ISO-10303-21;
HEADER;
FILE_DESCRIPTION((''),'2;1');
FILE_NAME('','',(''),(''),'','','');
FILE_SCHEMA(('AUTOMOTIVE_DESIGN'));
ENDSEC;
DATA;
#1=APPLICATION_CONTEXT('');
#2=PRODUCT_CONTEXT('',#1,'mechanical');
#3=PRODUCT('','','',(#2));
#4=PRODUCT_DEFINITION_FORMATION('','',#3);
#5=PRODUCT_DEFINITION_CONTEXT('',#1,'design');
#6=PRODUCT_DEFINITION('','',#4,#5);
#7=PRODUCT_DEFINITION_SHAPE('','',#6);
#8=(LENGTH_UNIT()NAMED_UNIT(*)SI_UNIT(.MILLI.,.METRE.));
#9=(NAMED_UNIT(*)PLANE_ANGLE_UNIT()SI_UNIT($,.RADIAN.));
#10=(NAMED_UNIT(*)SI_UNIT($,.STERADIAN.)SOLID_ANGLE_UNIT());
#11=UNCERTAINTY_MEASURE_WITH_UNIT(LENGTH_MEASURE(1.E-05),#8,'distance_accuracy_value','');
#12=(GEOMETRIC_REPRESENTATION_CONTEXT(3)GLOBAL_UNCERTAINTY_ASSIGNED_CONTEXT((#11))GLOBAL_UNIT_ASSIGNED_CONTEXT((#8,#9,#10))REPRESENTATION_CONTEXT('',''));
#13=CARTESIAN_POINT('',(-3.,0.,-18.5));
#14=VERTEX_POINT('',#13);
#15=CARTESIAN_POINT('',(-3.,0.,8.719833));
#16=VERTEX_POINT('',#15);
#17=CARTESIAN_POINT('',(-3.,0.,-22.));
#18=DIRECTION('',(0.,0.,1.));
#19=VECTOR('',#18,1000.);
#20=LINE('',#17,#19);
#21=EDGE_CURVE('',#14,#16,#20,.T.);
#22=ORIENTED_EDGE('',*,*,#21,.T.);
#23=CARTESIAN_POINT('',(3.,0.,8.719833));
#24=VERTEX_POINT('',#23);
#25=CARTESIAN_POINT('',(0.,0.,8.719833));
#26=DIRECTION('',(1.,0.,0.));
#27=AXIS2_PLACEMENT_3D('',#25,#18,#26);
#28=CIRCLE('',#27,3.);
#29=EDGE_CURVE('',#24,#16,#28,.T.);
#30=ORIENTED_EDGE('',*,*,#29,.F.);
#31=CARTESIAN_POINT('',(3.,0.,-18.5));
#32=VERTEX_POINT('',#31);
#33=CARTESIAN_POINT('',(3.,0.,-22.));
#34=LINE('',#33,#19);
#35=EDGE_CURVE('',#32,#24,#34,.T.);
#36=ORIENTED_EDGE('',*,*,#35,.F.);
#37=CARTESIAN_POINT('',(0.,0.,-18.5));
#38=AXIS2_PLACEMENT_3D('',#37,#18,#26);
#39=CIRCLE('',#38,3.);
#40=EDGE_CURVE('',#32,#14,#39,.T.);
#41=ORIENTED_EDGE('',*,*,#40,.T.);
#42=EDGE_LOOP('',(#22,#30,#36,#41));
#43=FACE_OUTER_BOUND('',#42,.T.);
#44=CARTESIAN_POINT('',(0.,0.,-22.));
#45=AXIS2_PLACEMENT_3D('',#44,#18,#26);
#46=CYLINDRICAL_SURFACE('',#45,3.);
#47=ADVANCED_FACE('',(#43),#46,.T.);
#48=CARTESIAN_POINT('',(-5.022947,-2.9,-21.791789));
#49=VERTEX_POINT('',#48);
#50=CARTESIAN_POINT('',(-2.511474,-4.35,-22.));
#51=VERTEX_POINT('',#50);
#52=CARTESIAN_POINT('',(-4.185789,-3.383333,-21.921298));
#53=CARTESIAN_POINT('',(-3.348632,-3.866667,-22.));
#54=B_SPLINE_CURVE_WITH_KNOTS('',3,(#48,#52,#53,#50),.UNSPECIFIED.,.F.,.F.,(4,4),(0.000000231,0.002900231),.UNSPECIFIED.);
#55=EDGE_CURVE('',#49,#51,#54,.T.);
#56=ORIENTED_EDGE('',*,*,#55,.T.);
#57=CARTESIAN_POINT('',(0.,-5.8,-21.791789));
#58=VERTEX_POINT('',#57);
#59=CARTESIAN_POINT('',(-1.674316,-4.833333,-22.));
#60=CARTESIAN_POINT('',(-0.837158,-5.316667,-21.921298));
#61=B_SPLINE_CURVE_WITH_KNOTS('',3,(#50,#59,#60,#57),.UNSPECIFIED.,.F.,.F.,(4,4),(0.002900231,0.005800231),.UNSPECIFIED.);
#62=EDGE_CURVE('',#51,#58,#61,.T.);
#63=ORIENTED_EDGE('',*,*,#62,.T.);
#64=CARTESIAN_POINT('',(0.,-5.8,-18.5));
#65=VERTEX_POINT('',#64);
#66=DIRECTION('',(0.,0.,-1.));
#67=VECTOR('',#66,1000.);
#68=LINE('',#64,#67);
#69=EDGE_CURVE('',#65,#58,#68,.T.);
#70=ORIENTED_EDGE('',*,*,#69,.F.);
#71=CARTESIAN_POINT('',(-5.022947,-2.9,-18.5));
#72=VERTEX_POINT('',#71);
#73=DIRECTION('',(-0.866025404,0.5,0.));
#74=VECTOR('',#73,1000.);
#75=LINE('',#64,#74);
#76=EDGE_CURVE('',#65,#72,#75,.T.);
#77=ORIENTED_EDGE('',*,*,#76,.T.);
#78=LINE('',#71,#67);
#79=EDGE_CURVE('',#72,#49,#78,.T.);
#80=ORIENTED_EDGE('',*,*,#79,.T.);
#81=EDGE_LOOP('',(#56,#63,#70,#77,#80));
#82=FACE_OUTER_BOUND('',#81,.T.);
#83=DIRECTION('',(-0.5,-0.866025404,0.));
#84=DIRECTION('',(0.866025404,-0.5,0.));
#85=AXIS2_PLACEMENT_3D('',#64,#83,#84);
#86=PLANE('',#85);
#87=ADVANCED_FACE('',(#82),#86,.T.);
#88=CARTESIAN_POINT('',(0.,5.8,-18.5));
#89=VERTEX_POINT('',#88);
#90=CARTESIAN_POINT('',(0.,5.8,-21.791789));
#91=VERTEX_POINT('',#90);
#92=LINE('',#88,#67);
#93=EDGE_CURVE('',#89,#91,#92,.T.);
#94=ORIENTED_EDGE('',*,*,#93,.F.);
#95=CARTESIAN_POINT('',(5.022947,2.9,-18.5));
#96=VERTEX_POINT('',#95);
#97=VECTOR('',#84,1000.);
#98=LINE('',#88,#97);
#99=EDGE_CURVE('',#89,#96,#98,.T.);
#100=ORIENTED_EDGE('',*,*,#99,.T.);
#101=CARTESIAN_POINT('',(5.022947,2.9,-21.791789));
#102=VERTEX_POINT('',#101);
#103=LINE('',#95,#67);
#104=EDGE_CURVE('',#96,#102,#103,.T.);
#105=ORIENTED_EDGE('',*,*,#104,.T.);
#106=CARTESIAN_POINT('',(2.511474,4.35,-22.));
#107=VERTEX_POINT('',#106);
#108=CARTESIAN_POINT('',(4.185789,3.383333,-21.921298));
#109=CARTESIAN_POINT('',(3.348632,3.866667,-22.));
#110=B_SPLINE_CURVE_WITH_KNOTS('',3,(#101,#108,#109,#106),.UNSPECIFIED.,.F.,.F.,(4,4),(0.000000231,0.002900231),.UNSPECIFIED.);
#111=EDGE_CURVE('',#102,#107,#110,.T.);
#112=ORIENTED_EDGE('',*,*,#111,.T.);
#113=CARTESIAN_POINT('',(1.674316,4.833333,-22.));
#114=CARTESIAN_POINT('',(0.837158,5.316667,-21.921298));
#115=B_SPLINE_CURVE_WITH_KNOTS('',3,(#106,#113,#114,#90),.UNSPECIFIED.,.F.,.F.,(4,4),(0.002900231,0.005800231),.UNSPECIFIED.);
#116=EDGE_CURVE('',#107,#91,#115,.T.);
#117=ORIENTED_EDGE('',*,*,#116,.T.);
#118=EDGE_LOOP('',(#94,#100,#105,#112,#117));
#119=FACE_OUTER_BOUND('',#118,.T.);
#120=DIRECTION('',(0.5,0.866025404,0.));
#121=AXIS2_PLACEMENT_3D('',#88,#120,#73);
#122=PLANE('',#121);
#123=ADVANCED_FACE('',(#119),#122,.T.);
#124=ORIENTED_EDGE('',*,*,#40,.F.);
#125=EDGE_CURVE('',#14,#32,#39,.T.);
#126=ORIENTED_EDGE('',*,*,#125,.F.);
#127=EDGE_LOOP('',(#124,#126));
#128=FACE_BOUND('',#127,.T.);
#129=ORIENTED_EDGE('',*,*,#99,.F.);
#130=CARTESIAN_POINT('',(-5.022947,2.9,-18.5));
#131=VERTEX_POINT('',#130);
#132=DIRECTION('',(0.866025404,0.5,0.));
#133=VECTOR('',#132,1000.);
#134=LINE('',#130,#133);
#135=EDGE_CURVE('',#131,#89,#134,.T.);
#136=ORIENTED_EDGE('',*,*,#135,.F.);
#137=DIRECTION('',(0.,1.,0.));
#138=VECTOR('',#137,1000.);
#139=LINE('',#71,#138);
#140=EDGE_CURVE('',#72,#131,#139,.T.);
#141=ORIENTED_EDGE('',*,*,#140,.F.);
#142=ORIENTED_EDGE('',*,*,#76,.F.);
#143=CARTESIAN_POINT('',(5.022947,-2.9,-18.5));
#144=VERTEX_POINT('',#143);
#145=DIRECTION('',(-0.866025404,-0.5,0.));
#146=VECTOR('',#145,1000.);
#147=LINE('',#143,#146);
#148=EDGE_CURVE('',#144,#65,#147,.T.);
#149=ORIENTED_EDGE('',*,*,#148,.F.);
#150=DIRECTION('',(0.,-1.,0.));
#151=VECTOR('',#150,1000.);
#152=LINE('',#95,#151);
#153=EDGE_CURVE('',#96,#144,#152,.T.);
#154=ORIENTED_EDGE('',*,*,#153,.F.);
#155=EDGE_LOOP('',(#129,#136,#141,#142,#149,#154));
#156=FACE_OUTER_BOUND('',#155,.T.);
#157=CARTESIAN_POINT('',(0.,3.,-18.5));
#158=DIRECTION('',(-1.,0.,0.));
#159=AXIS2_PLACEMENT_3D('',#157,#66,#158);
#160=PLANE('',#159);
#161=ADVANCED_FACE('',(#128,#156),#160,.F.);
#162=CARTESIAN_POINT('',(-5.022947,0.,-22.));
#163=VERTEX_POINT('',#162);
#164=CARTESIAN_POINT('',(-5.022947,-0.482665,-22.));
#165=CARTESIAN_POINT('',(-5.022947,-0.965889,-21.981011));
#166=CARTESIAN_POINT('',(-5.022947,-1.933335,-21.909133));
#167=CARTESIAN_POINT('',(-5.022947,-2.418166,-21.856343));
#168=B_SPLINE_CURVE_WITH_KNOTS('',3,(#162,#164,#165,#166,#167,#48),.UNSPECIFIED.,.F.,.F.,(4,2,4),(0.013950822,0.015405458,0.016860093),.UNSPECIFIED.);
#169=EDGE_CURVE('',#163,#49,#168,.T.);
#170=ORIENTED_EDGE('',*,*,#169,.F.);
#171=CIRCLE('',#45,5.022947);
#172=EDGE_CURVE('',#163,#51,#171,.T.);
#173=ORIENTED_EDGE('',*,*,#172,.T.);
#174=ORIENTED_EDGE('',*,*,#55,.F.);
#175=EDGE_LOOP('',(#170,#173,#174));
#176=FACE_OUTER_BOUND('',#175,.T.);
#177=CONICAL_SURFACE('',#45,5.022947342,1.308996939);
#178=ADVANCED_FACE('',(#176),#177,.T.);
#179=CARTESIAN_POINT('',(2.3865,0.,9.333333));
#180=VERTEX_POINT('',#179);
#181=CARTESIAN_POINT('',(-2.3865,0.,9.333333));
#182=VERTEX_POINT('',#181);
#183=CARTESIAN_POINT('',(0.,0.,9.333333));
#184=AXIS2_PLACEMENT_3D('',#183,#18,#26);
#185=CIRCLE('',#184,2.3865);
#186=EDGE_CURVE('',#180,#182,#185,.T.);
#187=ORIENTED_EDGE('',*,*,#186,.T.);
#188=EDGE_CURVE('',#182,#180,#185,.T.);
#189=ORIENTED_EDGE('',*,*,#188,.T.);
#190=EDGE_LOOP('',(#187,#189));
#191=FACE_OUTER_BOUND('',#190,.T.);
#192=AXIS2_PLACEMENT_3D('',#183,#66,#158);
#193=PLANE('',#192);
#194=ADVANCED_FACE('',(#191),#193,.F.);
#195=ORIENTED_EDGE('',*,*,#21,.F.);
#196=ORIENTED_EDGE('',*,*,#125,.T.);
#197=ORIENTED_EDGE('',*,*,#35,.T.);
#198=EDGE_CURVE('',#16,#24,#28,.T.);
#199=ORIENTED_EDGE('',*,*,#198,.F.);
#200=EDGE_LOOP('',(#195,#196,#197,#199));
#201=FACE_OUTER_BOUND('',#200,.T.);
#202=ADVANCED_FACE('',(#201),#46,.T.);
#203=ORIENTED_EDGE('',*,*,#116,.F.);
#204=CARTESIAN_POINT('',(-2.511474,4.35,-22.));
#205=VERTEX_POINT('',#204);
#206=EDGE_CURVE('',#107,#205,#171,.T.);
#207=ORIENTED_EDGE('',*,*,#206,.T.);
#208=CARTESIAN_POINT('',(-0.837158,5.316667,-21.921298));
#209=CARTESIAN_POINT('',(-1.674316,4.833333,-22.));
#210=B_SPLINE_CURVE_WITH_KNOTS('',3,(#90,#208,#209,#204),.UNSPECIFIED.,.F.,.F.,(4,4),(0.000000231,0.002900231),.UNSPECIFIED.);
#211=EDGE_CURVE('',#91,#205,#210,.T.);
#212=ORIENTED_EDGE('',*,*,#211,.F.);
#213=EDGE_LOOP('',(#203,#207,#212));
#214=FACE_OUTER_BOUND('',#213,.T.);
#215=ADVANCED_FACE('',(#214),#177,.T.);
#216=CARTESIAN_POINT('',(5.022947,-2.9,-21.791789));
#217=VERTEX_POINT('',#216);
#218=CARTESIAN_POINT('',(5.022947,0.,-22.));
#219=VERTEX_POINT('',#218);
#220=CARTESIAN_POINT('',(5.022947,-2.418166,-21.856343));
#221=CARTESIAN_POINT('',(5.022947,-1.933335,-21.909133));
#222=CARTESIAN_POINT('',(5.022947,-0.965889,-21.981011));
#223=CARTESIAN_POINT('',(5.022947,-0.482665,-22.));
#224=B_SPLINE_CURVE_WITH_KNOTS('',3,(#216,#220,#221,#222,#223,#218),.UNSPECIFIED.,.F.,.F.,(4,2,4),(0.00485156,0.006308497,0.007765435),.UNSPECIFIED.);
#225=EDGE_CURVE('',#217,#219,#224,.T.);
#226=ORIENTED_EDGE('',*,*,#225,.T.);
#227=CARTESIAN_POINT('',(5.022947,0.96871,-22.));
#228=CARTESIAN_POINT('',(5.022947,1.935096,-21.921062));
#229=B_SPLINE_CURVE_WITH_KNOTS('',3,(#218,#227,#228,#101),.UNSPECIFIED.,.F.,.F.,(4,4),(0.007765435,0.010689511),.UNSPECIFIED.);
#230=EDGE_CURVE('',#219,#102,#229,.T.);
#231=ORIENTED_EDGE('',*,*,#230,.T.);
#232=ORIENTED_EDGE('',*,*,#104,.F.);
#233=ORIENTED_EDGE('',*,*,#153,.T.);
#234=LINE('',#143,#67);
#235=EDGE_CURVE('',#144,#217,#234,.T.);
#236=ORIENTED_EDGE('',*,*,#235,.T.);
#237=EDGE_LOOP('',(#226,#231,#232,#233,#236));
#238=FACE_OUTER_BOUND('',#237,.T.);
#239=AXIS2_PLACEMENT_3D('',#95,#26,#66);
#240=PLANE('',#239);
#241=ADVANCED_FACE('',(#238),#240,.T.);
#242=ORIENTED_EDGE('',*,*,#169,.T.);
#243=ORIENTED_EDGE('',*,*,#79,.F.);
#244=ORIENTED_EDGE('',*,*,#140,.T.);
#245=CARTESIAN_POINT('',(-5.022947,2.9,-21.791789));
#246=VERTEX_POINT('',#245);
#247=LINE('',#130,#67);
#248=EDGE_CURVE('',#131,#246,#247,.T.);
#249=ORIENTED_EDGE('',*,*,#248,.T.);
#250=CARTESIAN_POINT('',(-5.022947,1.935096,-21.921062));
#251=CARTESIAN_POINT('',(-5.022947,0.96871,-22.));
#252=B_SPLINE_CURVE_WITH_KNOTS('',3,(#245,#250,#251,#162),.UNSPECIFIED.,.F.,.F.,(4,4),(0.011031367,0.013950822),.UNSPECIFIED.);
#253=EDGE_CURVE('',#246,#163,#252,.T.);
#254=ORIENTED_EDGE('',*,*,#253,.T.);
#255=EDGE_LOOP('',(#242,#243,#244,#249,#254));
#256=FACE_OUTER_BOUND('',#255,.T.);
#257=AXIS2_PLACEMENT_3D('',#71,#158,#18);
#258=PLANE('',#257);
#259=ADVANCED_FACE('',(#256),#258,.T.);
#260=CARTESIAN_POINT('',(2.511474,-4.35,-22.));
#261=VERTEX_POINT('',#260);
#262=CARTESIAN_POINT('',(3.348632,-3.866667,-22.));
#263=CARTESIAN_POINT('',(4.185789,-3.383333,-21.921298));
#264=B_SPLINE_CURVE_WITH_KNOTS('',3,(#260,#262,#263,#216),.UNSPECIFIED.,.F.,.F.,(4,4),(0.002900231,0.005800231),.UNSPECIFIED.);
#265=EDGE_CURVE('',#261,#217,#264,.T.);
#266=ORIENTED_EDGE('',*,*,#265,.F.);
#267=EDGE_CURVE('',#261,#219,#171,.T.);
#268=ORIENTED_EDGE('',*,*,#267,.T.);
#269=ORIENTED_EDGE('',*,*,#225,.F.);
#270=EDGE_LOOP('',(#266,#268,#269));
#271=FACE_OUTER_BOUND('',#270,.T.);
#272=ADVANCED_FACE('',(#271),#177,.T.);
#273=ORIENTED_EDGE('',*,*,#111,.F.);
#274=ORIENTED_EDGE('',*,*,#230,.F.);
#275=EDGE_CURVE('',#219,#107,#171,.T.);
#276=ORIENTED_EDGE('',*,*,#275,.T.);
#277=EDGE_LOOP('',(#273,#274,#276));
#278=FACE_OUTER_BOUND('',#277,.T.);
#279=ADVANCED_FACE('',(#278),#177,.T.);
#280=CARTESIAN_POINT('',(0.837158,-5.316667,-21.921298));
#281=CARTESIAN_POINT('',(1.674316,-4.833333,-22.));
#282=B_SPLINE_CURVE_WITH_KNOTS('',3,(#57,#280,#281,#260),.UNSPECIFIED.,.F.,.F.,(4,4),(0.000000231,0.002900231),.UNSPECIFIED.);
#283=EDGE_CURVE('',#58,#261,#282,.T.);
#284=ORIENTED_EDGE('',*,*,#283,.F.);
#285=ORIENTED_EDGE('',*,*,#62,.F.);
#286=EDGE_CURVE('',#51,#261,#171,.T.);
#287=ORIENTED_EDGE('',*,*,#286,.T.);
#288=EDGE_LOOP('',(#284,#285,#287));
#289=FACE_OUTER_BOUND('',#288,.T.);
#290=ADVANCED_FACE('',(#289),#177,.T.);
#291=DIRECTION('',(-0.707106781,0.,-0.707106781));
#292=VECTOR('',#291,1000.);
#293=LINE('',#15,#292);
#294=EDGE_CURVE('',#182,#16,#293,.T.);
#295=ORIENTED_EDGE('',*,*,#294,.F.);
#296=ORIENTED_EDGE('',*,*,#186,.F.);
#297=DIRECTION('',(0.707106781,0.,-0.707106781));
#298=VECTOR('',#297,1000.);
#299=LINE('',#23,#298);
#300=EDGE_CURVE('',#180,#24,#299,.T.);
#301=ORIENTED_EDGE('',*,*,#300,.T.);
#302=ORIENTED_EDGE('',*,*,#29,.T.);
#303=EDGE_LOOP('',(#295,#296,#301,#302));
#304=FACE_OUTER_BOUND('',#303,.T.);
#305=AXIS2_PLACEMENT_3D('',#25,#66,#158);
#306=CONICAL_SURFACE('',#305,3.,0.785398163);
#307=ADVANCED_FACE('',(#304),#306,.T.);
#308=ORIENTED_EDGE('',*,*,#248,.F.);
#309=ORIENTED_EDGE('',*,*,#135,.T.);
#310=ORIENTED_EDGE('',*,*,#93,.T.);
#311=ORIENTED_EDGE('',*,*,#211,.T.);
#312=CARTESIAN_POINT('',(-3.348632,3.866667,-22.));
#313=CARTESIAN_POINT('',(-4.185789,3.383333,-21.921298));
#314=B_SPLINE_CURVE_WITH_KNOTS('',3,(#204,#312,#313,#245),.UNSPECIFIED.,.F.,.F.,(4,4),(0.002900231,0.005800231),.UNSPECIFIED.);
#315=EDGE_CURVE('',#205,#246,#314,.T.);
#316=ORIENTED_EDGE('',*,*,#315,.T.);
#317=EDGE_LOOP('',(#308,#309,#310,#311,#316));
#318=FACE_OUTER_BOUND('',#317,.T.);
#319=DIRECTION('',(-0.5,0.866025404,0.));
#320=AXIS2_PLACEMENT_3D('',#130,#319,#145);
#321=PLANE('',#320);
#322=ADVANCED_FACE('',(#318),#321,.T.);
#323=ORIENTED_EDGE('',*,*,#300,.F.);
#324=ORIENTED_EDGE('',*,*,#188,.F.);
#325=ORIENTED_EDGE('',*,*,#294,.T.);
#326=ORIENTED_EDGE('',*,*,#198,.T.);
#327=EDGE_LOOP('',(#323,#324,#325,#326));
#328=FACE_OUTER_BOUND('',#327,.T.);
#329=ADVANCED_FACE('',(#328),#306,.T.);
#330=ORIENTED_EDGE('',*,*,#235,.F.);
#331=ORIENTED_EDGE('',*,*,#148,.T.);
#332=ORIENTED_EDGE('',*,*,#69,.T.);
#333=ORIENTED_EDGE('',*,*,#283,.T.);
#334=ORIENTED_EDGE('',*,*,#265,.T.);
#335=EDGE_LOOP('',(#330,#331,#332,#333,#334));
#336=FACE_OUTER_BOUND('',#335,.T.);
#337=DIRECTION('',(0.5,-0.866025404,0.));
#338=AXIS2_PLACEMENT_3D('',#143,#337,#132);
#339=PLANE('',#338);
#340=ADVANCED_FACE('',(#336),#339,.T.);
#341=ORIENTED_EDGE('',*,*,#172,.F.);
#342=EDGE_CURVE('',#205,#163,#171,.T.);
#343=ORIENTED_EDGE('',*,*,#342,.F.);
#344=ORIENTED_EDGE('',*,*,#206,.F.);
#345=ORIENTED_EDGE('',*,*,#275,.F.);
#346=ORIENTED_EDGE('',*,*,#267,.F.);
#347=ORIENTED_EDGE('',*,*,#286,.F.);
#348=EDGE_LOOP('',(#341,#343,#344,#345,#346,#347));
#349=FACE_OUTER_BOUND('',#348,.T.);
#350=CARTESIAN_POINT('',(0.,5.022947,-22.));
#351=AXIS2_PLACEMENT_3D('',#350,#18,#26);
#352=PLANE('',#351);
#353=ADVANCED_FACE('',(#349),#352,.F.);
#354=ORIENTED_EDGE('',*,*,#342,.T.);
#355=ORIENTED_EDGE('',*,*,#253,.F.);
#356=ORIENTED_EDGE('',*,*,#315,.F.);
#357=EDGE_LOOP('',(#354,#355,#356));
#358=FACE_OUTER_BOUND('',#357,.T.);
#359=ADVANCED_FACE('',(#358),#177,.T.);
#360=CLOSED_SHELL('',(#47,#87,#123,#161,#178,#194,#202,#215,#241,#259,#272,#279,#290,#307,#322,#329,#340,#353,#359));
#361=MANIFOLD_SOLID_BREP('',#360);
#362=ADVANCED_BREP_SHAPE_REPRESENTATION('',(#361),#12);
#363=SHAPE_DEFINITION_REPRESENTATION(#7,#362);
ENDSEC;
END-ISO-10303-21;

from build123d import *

# Parameters (mm, degrees)
SKETCH_2_R          = 11.6
CUT_EXTRUDE_1_DEPTH = 3.5


with BuildPart() as part:
    # 草图1 → 旋转1 (revolve)
    with BuildSketch(Plane(origin=(0, 0, 0), x_dir=(0, 0, -1), z_dir=(1, 0, 0)), mode=Mode.PRIVATE) as revolve_1_sk:
        Polygon((-9.333333333, 0), (-9.333333333, 2.3865), (-8.719833333, 3), (18.5, 3), (18.5, 5.8), (21.791789368, 5.8), (22, 5.022947342), (22, 0), align=None)
    revolve(revolve_1_sk.sketch.rotate(Axis((0, 0, -22), (0, 0, 1)), 270), axis=Axis((0, 0, -22), (0, 0, 1)))

    # 草图2 → 切除-拉伸1 (cut)
    with BuildSketch(Plane(origin=(0, 0, -22), x_dir=(-1, 0, 0), z_dir=(0, 0, -1))):
        Circle(SKETCH_2_R)
        Polygon((0, -5.8), (5.022947342, -2.9), (5.022947342, 2.9), (0, 5.8), (-5.022947342, 2.9), (-5.022947342, -2.9), align=None, mode=Mode.SUBTRACT)
    extrude(amount=-CUT_EXTRUDE_1_DEPTH, mode=Mode.SUBTRACT)


solid = part.part
